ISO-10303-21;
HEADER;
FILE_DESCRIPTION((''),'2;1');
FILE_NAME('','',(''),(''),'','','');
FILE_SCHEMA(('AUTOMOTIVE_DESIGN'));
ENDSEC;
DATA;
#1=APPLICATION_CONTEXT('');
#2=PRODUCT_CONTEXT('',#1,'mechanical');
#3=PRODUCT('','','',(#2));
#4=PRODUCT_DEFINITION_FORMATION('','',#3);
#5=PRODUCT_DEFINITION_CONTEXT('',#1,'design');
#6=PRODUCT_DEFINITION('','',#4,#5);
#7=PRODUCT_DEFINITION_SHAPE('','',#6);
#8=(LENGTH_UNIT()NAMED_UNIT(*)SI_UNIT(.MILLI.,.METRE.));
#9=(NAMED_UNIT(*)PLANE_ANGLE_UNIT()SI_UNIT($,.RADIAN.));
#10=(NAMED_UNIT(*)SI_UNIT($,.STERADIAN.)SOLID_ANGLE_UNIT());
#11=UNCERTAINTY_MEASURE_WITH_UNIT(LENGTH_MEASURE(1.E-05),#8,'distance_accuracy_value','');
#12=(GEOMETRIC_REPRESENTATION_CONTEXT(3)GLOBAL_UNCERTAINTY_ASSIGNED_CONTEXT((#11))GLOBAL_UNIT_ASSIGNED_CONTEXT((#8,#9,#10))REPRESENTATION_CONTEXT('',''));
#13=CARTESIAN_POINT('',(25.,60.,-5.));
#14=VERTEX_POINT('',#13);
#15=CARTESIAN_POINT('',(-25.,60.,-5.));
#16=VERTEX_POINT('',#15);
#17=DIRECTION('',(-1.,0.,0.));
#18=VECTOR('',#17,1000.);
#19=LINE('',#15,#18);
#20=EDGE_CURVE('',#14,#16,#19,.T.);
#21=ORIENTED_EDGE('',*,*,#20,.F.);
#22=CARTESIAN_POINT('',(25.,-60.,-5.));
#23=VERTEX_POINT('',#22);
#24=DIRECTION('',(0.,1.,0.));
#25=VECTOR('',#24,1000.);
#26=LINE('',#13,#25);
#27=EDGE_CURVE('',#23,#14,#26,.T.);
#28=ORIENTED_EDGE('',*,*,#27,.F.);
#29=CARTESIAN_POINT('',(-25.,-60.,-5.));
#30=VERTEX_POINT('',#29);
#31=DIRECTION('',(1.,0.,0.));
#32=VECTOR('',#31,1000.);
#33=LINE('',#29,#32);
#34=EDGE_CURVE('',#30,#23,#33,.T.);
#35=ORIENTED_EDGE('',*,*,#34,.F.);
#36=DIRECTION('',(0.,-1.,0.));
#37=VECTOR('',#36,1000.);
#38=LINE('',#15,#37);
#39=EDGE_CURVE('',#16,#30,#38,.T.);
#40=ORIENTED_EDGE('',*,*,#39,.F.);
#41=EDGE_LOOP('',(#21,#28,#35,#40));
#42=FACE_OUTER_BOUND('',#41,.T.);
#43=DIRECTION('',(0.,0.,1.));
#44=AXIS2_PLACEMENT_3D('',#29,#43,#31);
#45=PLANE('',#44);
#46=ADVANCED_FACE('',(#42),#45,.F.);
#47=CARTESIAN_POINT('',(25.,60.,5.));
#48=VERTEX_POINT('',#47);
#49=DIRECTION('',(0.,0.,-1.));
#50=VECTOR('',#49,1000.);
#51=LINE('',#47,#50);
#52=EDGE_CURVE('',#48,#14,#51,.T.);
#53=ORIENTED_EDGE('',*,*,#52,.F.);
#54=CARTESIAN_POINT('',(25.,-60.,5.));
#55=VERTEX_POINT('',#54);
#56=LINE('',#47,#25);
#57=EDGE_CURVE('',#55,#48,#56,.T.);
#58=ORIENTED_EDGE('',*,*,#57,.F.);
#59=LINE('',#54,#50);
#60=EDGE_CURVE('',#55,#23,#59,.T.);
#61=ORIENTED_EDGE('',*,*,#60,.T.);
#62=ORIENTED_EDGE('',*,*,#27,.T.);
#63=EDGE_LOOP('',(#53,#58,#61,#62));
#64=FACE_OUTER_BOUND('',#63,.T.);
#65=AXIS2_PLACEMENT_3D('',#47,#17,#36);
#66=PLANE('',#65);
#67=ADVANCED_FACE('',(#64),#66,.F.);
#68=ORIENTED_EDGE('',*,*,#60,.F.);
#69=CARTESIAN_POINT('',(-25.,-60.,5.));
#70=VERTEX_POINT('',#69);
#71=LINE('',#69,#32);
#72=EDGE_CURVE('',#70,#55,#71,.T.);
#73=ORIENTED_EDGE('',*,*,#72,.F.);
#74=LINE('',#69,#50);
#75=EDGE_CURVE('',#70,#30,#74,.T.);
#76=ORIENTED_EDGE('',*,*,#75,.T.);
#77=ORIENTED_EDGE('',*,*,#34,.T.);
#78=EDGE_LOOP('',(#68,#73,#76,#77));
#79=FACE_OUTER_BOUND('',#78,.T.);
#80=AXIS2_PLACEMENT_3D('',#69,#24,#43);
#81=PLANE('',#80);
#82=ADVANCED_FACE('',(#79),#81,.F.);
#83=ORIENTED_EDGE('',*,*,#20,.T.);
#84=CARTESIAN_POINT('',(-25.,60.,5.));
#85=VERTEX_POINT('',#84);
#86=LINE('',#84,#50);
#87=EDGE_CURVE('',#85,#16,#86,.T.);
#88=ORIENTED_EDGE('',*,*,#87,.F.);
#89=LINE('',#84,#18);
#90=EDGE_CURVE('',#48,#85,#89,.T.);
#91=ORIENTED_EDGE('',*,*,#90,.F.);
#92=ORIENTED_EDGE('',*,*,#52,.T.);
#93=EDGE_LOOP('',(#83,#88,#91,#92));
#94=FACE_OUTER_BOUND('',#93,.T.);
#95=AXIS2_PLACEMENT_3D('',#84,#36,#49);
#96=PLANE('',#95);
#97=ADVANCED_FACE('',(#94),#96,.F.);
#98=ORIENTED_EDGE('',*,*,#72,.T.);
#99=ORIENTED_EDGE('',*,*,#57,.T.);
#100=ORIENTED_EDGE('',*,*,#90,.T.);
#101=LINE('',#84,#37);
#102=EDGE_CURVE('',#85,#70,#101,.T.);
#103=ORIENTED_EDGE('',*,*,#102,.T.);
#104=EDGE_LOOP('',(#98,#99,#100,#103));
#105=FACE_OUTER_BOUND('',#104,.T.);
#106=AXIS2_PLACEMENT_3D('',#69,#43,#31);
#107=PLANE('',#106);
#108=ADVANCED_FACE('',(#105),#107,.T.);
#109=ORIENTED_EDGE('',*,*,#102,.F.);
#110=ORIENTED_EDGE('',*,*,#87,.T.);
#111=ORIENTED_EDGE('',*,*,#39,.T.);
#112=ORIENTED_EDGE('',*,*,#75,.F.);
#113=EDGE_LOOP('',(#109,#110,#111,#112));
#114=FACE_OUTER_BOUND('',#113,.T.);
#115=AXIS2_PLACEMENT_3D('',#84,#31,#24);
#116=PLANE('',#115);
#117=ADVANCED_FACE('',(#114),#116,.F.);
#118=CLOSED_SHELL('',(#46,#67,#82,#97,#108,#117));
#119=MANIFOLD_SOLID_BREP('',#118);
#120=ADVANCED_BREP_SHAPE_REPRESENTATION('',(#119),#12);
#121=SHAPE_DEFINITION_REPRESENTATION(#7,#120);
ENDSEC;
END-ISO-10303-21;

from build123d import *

# Parameters (mm, degrees)
SKETCH1_W           = 50
SKETCH1_H           = 120
BOSS_EXTRUDE1_DEPTH = 5


with BuildPart() as part:
    # Sketch1 → Boss-Extrude1 (new, symmetric)
    with BuildSketch(Plane.XY):
        Rectangle(SKETCH1_W, SKETCH1_H)
    extrude(amount=BOSS_EXTRUDE1_DEPTH, both=True)


solid = part.part
